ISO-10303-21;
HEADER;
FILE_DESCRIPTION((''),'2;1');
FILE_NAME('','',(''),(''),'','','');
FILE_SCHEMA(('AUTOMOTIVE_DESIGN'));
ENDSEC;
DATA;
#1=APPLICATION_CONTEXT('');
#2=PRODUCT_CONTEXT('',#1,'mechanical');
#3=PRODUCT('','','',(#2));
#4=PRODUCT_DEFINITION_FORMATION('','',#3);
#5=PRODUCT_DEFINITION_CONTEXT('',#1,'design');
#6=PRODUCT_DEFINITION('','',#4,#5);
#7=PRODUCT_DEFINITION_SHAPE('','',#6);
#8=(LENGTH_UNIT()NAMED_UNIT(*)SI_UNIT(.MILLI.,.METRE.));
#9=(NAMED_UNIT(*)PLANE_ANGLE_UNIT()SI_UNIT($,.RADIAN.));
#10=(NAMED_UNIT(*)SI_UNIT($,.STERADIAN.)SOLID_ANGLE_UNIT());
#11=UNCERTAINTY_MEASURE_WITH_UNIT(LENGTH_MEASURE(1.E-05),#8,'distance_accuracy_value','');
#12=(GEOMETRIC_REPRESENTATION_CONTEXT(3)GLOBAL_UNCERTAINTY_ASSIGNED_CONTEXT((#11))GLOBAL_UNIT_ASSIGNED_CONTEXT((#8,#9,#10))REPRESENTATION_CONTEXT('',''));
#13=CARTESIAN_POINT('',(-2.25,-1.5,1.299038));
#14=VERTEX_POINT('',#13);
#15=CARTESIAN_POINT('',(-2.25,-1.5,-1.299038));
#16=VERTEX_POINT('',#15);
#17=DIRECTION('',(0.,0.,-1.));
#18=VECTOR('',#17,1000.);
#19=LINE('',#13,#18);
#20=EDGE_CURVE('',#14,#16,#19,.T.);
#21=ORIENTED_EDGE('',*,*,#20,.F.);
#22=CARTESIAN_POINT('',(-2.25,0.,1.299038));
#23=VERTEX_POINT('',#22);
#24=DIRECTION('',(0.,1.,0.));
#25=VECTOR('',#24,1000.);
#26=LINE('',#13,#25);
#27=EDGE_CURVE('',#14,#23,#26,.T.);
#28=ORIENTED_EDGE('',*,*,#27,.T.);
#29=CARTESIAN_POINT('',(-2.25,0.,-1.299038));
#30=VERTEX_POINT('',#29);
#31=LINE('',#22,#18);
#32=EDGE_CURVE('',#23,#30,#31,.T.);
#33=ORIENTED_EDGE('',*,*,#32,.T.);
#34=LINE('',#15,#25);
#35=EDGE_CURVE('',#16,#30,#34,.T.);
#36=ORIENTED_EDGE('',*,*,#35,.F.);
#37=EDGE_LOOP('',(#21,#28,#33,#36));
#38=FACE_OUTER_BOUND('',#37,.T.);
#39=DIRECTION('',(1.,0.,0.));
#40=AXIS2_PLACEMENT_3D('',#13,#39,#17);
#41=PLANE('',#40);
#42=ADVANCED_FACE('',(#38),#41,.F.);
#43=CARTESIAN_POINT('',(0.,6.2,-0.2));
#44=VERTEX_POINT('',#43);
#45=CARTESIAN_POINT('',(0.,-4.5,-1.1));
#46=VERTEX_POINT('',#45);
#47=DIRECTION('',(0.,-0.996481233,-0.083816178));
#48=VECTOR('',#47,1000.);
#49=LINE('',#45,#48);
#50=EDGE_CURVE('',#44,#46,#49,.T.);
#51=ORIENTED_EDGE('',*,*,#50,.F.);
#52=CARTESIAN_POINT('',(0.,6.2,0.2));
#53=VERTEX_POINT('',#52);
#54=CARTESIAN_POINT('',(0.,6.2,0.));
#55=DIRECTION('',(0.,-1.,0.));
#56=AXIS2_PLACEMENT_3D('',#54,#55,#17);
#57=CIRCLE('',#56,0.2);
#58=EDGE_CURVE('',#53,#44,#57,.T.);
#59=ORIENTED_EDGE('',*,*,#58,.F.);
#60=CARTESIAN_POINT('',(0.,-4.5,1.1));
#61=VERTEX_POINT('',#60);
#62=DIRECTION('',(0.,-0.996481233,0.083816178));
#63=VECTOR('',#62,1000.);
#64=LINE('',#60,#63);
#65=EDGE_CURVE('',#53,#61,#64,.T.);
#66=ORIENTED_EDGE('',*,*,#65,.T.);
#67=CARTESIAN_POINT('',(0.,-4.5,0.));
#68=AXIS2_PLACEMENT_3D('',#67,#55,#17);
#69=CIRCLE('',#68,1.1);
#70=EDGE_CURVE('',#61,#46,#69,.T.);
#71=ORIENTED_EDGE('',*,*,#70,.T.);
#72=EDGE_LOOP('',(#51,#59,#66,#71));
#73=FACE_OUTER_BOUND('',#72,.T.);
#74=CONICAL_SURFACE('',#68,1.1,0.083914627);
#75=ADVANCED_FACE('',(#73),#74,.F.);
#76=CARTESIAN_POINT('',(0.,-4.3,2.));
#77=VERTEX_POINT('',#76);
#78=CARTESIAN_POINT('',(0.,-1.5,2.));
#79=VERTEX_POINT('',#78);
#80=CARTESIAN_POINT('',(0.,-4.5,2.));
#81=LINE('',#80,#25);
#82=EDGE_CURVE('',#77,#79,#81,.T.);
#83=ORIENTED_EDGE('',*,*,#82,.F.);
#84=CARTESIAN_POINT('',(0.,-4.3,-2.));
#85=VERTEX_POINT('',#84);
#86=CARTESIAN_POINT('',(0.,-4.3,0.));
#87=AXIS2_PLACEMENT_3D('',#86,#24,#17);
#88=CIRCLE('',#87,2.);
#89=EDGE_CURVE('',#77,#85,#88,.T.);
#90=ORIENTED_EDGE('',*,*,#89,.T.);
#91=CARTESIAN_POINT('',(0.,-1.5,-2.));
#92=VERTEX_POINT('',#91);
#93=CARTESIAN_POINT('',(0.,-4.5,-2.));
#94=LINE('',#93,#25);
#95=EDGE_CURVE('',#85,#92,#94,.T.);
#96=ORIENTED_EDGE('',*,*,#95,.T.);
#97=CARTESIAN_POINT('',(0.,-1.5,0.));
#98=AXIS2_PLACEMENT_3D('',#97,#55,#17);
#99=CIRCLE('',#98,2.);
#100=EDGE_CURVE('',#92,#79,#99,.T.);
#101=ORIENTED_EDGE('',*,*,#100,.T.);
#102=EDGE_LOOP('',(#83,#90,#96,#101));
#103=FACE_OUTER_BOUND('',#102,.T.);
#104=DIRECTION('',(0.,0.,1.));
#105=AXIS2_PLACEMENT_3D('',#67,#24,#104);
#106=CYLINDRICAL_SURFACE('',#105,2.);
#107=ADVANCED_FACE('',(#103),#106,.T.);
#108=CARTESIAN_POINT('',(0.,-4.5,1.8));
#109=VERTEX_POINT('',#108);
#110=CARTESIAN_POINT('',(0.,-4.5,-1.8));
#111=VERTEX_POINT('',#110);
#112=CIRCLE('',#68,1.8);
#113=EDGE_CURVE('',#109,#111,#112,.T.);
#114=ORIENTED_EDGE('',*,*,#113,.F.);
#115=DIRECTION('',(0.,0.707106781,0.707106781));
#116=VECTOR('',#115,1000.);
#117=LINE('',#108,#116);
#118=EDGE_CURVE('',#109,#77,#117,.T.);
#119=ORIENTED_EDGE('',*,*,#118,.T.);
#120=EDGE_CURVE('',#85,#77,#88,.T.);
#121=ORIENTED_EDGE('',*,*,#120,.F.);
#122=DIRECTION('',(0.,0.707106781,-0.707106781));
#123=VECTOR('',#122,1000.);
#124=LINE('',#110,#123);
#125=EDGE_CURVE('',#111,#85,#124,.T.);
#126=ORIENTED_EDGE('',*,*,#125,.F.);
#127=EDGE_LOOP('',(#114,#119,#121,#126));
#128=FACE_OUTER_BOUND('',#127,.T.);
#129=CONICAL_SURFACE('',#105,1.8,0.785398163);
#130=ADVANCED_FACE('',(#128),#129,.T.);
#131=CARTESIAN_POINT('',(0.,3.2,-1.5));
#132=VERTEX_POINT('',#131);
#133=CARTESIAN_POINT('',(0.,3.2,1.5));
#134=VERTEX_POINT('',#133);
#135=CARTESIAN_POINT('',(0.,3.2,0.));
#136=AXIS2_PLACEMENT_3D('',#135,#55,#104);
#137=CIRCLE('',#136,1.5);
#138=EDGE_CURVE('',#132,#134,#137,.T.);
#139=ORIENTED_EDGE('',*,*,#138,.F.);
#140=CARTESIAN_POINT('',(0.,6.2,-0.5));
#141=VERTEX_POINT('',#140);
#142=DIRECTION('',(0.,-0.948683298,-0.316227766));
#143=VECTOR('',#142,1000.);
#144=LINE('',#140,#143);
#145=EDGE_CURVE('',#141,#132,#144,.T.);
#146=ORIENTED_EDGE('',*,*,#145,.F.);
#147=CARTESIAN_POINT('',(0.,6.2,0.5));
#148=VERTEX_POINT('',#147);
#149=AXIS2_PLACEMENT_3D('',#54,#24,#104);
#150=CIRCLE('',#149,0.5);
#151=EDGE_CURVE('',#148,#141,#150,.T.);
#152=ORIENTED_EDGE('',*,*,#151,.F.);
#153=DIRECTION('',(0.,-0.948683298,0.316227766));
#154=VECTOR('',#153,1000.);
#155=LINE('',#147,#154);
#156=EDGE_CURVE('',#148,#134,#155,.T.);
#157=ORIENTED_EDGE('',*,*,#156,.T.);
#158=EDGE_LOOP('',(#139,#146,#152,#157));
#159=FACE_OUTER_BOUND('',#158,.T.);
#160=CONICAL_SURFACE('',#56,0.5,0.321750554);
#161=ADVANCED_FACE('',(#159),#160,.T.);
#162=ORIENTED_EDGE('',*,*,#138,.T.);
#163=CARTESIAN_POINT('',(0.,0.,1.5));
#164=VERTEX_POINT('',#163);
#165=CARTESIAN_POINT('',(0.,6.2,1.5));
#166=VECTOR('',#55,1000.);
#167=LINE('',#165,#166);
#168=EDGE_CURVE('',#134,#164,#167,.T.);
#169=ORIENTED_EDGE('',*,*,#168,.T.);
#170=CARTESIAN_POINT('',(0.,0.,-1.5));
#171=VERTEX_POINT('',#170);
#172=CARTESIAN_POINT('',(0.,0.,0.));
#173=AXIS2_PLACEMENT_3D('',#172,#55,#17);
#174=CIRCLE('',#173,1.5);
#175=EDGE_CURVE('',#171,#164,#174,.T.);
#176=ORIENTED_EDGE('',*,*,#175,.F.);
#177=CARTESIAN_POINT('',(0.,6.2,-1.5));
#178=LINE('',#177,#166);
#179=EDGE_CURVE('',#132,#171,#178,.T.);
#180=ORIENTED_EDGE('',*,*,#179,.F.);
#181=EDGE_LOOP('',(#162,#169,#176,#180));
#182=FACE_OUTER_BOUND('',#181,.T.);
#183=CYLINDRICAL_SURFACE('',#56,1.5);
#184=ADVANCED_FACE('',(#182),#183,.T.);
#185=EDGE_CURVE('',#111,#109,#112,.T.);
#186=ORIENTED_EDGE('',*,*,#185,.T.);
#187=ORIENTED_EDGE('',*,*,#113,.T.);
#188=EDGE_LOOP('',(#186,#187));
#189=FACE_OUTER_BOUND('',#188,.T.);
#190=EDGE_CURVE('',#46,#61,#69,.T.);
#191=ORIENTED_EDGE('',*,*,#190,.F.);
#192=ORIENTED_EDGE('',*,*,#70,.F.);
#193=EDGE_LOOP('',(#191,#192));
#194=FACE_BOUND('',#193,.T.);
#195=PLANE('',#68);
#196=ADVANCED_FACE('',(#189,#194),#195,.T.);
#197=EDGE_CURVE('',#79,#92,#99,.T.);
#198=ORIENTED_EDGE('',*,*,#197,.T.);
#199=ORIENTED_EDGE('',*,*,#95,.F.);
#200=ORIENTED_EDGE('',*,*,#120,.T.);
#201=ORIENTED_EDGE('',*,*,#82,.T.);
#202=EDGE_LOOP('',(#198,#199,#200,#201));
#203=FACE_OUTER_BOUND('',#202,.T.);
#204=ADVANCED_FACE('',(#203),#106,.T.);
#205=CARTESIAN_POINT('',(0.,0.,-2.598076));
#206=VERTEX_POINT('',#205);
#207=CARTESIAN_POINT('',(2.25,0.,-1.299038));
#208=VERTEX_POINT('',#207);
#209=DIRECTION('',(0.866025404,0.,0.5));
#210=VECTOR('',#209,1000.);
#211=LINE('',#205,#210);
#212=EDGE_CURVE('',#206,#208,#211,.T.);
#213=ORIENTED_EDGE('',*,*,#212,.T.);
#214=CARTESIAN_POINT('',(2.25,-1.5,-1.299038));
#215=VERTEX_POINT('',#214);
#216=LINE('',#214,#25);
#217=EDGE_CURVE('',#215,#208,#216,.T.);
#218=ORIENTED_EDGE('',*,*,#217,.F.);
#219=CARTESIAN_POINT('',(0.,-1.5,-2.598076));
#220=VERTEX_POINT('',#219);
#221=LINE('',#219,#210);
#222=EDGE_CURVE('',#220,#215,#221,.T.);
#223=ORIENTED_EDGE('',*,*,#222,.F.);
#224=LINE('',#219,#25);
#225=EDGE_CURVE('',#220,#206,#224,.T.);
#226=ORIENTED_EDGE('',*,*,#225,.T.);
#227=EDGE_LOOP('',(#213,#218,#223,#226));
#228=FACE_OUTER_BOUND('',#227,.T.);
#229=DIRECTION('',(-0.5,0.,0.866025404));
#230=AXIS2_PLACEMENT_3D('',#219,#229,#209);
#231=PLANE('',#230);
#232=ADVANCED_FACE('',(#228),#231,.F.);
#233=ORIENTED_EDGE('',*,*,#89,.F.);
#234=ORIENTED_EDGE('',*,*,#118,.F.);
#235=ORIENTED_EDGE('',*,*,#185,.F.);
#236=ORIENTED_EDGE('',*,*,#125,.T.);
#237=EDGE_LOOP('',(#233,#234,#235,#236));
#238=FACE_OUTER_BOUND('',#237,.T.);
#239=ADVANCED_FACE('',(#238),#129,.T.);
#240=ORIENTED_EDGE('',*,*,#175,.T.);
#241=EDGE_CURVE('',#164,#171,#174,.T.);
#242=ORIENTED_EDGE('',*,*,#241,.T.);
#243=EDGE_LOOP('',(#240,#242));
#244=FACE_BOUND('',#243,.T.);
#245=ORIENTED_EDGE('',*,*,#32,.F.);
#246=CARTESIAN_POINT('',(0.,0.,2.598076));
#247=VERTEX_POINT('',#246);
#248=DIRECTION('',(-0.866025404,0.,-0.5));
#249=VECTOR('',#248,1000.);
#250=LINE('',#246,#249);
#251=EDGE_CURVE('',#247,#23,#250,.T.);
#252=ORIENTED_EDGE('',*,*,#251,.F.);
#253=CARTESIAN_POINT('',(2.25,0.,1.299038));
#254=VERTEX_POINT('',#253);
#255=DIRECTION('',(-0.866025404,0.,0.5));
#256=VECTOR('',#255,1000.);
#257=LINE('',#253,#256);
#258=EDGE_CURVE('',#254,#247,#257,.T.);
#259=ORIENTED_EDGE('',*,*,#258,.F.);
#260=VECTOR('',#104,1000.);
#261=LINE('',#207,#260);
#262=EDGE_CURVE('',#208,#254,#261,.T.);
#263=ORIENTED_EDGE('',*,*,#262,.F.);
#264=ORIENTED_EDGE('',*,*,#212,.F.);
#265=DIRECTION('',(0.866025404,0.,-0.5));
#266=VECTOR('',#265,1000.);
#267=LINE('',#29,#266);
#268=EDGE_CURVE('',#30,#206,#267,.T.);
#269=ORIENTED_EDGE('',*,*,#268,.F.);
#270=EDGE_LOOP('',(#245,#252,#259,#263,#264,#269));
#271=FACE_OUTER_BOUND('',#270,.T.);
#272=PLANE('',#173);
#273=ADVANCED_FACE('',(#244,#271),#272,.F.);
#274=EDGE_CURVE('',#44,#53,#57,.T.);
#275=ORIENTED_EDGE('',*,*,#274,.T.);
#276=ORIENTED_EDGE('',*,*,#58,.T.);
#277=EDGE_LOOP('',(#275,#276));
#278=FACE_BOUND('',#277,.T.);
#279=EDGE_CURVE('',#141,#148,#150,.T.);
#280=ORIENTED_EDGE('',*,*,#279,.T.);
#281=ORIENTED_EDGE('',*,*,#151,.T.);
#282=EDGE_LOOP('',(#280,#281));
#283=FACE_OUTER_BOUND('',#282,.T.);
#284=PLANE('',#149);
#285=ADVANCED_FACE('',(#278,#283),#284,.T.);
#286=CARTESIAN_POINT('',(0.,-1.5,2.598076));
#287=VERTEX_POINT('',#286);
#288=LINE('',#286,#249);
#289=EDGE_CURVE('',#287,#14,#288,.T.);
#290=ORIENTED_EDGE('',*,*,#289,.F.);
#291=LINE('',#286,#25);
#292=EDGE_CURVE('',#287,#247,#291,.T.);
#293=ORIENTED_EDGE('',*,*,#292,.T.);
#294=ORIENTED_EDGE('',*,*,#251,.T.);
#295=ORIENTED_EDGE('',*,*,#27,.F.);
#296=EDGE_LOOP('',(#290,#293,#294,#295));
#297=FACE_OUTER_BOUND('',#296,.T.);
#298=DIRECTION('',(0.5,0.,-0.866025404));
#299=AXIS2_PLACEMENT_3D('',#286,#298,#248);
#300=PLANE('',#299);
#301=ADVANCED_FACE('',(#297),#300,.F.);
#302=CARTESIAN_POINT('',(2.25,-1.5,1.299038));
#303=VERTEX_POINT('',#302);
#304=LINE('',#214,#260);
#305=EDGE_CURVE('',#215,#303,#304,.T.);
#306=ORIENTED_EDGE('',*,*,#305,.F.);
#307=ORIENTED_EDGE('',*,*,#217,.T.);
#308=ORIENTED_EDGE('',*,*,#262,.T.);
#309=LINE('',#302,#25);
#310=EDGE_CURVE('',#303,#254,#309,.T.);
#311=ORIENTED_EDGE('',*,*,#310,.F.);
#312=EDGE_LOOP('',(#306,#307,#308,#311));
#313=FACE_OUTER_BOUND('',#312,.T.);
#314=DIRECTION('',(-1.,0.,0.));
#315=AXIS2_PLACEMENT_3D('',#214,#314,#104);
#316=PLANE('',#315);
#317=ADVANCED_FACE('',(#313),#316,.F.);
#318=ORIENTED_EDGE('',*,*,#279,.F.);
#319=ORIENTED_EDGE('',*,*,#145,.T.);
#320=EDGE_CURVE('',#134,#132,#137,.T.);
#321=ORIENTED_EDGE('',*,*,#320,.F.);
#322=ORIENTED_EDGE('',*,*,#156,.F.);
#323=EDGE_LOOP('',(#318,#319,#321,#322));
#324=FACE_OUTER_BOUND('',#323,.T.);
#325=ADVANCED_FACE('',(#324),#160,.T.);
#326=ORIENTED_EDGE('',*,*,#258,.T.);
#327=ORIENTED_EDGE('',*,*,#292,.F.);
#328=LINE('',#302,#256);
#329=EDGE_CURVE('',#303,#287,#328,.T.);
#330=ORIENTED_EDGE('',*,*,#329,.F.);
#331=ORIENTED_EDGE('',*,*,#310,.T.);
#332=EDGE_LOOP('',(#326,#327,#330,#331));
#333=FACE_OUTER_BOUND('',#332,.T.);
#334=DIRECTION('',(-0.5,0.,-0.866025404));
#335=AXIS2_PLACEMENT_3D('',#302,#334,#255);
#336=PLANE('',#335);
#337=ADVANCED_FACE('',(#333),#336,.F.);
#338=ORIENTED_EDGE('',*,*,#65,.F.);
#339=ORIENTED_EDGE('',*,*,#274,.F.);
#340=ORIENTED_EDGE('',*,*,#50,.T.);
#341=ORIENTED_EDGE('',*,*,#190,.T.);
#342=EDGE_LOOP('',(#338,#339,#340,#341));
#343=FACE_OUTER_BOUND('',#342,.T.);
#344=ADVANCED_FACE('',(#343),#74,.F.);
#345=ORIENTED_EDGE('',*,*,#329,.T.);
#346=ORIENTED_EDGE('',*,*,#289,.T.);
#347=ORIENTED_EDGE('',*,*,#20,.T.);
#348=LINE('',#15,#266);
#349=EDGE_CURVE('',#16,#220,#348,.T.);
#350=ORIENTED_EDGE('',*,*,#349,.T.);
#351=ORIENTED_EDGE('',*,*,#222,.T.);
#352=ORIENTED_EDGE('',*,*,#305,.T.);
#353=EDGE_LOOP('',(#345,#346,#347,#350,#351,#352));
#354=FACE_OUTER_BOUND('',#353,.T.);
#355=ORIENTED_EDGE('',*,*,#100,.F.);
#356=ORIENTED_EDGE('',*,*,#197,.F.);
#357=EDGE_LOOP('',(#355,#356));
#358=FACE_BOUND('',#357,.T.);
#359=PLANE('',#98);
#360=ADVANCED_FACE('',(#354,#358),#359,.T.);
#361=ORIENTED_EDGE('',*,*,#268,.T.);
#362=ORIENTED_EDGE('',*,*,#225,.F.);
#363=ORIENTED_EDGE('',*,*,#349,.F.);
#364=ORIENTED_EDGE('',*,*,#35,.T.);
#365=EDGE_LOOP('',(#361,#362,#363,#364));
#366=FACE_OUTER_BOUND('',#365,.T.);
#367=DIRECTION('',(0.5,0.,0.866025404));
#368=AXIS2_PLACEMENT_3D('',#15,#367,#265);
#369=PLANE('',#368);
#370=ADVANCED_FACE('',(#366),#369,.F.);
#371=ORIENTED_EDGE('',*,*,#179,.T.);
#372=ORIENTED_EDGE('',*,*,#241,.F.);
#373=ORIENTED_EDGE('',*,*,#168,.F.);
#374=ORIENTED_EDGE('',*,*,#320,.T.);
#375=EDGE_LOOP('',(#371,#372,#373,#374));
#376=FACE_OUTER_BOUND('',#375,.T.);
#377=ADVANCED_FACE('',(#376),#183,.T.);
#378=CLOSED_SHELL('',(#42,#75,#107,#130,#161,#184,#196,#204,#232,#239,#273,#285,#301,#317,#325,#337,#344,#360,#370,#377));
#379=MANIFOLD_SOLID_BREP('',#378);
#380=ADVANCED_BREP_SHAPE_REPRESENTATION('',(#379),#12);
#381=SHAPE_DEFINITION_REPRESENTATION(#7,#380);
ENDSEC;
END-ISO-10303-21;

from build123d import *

# Parameters (mm, degrees)
SKETCH1_R           = 1.5
BOSS_EXTRUDE1_DEPTH = 6.2
SKETCH3_R           = 0.2
CUT_EXTRUDE2_DEPTH  = 7.55286197
CHAMFER1_SIZE       = 3
CHAMFER1_SIZE2      = 1
SKETCH5_R           = 0.5
CUT_EXTRUDE3_DEPTH  = 1.5
BOSS_EXTRUDE2_START = 1.5
SKETCH7_R           = 0.5
BOSS_EXTRUDE2_DEPTH = 1.5
BOSS_EXTRUDE3_START = 3
SKETCH8_R           = 2
SKETCH8_R_2         = 0.5
BOSS_EXTRUDE3_DEPTH = 3
CHAMFER4_SIZE       = 0.2


with BuildPart() as part:
    # Sketch1 → Boss-Extrude1 (new body)
    with BuildSketch(Plane(origin=(0, 0, 0), x_dir=(1, 0, 0), z_dir=(0, 1, 0))):
        with Locations(Location((0, 0, 0), (0, 0, 90))):
            Circle(SKETCH1_R)
    extrude(amount=BOSS_EXTRUDE1_DEPTH)

    # Sketch3 → Cut-Extrude2 (cut, through all)
    with BuildSketch(Plane(origin=(0, 6.2, 0), x_dir=(1, 0, 0), z_dir=(0, 1, 0))):
        with Locations(Location((0, 0, 0), (0, 0, 270))):
            Circle(SKETCH3_R)
    extrude(amount=-CUT_EXTRUDE2_DEPTH, mode=Mode.SUBTRACT)

    # Chamfer1
    chamfer1_edges = [part.edges().sort_by_distance(p)[0] for p in [
        (0, 6.2, 1.5),
    ]]
    chamfer1_side = [part.faces().sort_by_distance(p)[0] for p in [
        (0, 3.1, 1.5),
    ]]
    chamfer(chamfer1_edges, length=CHAMFER1_SIZE, length2=CHAMFER1_SIZE2, reference=chamfer1_side[0])

    # Sketch5 → Cut-Extrude3 (cut)
    with BuildSketch(Plane.XZ):
        with Locations(Location((0, 0, 0), (0, 0, 270))):
            Circle(SKETCH5_R)
    extrude(amount=-CUT_EXTRUDE3_DEPTH, mode=Mode.SUBTRACT)

    # Sketch7 → Boss-Extrude2 (add)
    with BuildSketch(Plane.XZ.offset(BOSS_EXTRUDE2_START)):
        Polygon((0, 2.598076211), (-2.25, 1.299038106), (-2.25, -1.299038106), (0, -2.598076211), (2.25, -1.299038106), (2.25, 1.299038106), align=None)
        with Locations(Location((0, 0, 0), (0, 0, 270))):
            Circle(SKETCH7_R, mode=Mode.SUBTRACT)
    extrude(amount=-BOSS_EXTRUDE2_DEPTH)

    # Sketch8 → Boss-Extrude3 (add)
    with BuildSketch(Plane.XZ.offset(1.5).offset(BOSS_EXTRUDE3_START)):
        with Locations(Location((0, 0, 0), (0, 0, 270))):
            Circle(SKETCH8_R)
        with Locations(Location((0, 0, 0), (0, 0, 270))):
            Circle(SKETCH8_R_2, mode=Mode.SUBTRACT)
    extrude(amount=-BOSS_EXTRUDE3_DEPTH)

    # Sketch9 → Cut-Revolve2 (revolve, cut)
    with BuildSketch(Plane.XY, mode=Mode.PRIVATE) as cut_revolve2_sk:
        Polygon((0.2, 6.2), (1.1, -4.5), (0, -4.5), (0, 6.2), align=None)
    revolve(cut_revolve2_sk.sketch.rotate(Axis((0, -1009.643261514, 0), (0, 1, 0)), 90), axis=Axis((0, -1009.643261514, 0), (0, 1, 0)), mode=Mode.SUBTRACT)

    # Chamfer4
    chamfer4_edges = [part.edges().sort_by_distance(p)[0] for p in [
        (0, -4.5, 2),
    ]]
    chamfer(chamfer4_edges, length=CHAMFER4_SIZE)


solid = part.part
